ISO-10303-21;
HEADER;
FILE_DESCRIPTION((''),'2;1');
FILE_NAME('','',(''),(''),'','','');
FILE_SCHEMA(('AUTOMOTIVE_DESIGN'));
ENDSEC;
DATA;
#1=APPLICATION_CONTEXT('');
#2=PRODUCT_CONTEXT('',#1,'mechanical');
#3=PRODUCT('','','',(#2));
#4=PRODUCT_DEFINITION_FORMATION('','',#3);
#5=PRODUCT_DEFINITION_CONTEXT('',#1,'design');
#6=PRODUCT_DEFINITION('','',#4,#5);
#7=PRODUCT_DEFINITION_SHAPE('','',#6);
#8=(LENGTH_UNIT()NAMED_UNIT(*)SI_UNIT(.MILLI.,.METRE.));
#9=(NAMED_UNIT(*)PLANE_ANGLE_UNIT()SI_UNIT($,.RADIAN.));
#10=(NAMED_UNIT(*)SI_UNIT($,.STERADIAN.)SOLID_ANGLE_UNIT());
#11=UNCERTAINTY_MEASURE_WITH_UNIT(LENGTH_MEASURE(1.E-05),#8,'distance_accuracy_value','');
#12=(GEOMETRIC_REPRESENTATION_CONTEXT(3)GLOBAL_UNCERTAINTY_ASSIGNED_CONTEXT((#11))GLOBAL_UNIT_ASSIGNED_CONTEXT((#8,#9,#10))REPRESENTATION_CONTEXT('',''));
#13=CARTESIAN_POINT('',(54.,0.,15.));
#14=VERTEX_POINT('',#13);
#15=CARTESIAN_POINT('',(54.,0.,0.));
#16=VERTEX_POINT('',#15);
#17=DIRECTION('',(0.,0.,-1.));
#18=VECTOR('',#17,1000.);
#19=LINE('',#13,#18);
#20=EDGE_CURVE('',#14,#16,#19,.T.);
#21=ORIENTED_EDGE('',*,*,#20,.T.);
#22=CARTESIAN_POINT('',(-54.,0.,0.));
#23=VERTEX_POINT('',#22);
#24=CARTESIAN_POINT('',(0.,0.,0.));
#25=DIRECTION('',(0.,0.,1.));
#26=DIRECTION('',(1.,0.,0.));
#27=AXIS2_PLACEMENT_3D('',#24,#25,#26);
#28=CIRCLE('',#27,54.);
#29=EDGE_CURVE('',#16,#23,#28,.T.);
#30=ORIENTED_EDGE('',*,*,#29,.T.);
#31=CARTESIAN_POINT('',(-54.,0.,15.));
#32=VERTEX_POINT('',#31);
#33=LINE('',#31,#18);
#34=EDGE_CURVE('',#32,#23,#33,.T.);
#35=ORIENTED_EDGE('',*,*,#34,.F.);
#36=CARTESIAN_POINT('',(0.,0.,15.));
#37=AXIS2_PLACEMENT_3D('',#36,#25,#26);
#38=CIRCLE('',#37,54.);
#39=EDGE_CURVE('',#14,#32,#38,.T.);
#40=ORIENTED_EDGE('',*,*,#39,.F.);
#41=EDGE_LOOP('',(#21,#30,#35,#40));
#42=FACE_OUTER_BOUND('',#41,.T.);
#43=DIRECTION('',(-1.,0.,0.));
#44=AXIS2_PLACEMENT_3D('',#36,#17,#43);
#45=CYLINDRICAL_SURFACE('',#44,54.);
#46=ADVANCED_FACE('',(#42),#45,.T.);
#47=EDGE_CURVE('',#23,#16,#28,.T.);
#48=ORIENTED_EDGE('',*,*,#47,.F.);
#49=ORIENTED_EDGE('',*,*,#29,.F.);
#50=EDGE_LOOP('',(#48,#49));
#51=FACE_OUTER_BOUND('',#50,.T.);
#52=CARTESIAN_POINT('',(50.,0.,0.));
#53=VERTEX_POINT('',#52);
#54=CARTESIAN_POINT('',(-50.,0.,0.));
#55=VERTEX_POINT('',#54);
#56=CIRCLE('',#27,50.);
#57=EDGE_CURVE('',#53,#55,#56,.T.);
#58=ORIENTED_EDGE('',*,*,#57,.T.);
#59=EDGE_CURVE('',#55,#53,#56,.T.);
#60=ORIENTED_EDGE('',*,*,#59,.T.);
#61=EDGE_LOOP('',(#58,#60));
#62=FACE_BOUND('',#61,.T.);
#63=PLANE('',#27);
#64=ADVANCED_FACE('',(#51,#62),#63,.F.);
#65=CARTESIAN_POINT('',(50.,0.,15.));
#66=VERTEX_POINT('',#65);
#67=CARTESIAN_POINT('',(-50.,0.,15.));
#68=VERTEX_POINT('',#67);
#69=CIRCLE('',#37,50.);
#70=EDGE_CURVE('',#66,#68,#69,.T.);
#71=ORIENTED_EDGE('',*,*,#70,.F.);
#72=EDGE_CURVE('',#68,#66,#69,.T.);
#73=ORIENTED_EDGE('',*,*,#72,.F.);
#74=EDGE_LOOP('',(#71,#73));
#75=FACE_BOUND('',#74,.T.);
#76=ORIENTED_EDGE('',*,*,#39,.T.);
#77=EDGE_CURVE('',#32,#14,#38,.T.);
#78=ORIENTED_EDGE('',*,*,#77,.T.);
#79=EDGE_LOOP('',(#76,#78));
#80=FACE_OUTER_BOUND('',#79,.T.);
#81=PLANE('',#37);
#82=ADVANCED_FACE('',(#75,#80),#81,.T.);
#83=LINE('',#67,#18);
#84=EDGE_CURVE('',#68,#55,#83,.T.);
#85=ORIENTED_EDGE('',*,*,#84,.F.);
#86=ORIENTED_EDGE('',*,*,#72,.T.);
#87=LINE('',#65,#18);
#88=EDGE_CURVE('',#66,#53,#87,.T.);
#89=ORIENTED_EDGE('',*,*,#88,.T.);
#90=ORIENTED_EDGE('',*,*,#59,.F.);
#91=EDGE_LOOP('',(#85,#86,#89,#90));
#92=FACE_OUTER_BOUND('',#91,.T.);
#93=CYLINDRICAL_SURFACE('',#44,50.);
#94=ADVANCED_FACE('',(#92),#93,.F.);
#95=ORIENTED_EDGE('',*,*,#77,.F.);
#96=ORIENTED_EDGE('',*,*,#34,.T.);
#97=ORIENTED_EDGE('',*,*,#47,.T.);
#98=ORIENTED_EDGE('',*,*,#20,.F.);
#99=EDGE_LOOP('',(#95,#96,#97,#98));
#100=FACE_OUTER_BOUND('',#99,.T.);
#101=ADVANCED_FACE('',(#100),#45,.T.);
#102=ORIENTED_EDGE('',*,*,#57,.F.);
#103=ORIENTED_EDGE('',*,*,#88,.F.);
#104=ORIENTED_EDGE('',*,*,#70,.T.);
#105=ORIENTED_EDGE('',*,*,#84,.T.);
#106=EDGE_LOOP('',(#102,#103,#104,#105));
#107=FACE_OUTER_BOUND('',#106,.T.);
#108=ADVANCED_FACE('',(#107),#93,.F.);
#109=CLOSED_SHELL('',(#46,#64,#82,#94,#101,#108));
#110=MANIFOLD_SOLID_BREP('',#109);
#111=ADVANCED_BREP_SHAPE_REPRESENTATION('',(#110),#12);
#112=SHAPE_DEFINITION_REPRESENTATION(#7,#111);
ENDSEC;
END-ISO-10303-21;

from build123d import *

# Parameters (mm, degrees)
SKETCH1_R           = 54
SKETCH1_R_2         = 50
BOSS_EXTRUDE1_DEPTH = 15


with BuildPart() as part:
    # Sketch1 → Boss-Extrude1 (new body)
    with BuildSketch(Plane.XY):
        Circle(SKETCH1_R)
        Circle(SKETCH1_R_2, mode=Mode.SUBTRACT)
    extrude(amount=BOSS_EXTRUDE1_DEPTH)


solid = part.part
